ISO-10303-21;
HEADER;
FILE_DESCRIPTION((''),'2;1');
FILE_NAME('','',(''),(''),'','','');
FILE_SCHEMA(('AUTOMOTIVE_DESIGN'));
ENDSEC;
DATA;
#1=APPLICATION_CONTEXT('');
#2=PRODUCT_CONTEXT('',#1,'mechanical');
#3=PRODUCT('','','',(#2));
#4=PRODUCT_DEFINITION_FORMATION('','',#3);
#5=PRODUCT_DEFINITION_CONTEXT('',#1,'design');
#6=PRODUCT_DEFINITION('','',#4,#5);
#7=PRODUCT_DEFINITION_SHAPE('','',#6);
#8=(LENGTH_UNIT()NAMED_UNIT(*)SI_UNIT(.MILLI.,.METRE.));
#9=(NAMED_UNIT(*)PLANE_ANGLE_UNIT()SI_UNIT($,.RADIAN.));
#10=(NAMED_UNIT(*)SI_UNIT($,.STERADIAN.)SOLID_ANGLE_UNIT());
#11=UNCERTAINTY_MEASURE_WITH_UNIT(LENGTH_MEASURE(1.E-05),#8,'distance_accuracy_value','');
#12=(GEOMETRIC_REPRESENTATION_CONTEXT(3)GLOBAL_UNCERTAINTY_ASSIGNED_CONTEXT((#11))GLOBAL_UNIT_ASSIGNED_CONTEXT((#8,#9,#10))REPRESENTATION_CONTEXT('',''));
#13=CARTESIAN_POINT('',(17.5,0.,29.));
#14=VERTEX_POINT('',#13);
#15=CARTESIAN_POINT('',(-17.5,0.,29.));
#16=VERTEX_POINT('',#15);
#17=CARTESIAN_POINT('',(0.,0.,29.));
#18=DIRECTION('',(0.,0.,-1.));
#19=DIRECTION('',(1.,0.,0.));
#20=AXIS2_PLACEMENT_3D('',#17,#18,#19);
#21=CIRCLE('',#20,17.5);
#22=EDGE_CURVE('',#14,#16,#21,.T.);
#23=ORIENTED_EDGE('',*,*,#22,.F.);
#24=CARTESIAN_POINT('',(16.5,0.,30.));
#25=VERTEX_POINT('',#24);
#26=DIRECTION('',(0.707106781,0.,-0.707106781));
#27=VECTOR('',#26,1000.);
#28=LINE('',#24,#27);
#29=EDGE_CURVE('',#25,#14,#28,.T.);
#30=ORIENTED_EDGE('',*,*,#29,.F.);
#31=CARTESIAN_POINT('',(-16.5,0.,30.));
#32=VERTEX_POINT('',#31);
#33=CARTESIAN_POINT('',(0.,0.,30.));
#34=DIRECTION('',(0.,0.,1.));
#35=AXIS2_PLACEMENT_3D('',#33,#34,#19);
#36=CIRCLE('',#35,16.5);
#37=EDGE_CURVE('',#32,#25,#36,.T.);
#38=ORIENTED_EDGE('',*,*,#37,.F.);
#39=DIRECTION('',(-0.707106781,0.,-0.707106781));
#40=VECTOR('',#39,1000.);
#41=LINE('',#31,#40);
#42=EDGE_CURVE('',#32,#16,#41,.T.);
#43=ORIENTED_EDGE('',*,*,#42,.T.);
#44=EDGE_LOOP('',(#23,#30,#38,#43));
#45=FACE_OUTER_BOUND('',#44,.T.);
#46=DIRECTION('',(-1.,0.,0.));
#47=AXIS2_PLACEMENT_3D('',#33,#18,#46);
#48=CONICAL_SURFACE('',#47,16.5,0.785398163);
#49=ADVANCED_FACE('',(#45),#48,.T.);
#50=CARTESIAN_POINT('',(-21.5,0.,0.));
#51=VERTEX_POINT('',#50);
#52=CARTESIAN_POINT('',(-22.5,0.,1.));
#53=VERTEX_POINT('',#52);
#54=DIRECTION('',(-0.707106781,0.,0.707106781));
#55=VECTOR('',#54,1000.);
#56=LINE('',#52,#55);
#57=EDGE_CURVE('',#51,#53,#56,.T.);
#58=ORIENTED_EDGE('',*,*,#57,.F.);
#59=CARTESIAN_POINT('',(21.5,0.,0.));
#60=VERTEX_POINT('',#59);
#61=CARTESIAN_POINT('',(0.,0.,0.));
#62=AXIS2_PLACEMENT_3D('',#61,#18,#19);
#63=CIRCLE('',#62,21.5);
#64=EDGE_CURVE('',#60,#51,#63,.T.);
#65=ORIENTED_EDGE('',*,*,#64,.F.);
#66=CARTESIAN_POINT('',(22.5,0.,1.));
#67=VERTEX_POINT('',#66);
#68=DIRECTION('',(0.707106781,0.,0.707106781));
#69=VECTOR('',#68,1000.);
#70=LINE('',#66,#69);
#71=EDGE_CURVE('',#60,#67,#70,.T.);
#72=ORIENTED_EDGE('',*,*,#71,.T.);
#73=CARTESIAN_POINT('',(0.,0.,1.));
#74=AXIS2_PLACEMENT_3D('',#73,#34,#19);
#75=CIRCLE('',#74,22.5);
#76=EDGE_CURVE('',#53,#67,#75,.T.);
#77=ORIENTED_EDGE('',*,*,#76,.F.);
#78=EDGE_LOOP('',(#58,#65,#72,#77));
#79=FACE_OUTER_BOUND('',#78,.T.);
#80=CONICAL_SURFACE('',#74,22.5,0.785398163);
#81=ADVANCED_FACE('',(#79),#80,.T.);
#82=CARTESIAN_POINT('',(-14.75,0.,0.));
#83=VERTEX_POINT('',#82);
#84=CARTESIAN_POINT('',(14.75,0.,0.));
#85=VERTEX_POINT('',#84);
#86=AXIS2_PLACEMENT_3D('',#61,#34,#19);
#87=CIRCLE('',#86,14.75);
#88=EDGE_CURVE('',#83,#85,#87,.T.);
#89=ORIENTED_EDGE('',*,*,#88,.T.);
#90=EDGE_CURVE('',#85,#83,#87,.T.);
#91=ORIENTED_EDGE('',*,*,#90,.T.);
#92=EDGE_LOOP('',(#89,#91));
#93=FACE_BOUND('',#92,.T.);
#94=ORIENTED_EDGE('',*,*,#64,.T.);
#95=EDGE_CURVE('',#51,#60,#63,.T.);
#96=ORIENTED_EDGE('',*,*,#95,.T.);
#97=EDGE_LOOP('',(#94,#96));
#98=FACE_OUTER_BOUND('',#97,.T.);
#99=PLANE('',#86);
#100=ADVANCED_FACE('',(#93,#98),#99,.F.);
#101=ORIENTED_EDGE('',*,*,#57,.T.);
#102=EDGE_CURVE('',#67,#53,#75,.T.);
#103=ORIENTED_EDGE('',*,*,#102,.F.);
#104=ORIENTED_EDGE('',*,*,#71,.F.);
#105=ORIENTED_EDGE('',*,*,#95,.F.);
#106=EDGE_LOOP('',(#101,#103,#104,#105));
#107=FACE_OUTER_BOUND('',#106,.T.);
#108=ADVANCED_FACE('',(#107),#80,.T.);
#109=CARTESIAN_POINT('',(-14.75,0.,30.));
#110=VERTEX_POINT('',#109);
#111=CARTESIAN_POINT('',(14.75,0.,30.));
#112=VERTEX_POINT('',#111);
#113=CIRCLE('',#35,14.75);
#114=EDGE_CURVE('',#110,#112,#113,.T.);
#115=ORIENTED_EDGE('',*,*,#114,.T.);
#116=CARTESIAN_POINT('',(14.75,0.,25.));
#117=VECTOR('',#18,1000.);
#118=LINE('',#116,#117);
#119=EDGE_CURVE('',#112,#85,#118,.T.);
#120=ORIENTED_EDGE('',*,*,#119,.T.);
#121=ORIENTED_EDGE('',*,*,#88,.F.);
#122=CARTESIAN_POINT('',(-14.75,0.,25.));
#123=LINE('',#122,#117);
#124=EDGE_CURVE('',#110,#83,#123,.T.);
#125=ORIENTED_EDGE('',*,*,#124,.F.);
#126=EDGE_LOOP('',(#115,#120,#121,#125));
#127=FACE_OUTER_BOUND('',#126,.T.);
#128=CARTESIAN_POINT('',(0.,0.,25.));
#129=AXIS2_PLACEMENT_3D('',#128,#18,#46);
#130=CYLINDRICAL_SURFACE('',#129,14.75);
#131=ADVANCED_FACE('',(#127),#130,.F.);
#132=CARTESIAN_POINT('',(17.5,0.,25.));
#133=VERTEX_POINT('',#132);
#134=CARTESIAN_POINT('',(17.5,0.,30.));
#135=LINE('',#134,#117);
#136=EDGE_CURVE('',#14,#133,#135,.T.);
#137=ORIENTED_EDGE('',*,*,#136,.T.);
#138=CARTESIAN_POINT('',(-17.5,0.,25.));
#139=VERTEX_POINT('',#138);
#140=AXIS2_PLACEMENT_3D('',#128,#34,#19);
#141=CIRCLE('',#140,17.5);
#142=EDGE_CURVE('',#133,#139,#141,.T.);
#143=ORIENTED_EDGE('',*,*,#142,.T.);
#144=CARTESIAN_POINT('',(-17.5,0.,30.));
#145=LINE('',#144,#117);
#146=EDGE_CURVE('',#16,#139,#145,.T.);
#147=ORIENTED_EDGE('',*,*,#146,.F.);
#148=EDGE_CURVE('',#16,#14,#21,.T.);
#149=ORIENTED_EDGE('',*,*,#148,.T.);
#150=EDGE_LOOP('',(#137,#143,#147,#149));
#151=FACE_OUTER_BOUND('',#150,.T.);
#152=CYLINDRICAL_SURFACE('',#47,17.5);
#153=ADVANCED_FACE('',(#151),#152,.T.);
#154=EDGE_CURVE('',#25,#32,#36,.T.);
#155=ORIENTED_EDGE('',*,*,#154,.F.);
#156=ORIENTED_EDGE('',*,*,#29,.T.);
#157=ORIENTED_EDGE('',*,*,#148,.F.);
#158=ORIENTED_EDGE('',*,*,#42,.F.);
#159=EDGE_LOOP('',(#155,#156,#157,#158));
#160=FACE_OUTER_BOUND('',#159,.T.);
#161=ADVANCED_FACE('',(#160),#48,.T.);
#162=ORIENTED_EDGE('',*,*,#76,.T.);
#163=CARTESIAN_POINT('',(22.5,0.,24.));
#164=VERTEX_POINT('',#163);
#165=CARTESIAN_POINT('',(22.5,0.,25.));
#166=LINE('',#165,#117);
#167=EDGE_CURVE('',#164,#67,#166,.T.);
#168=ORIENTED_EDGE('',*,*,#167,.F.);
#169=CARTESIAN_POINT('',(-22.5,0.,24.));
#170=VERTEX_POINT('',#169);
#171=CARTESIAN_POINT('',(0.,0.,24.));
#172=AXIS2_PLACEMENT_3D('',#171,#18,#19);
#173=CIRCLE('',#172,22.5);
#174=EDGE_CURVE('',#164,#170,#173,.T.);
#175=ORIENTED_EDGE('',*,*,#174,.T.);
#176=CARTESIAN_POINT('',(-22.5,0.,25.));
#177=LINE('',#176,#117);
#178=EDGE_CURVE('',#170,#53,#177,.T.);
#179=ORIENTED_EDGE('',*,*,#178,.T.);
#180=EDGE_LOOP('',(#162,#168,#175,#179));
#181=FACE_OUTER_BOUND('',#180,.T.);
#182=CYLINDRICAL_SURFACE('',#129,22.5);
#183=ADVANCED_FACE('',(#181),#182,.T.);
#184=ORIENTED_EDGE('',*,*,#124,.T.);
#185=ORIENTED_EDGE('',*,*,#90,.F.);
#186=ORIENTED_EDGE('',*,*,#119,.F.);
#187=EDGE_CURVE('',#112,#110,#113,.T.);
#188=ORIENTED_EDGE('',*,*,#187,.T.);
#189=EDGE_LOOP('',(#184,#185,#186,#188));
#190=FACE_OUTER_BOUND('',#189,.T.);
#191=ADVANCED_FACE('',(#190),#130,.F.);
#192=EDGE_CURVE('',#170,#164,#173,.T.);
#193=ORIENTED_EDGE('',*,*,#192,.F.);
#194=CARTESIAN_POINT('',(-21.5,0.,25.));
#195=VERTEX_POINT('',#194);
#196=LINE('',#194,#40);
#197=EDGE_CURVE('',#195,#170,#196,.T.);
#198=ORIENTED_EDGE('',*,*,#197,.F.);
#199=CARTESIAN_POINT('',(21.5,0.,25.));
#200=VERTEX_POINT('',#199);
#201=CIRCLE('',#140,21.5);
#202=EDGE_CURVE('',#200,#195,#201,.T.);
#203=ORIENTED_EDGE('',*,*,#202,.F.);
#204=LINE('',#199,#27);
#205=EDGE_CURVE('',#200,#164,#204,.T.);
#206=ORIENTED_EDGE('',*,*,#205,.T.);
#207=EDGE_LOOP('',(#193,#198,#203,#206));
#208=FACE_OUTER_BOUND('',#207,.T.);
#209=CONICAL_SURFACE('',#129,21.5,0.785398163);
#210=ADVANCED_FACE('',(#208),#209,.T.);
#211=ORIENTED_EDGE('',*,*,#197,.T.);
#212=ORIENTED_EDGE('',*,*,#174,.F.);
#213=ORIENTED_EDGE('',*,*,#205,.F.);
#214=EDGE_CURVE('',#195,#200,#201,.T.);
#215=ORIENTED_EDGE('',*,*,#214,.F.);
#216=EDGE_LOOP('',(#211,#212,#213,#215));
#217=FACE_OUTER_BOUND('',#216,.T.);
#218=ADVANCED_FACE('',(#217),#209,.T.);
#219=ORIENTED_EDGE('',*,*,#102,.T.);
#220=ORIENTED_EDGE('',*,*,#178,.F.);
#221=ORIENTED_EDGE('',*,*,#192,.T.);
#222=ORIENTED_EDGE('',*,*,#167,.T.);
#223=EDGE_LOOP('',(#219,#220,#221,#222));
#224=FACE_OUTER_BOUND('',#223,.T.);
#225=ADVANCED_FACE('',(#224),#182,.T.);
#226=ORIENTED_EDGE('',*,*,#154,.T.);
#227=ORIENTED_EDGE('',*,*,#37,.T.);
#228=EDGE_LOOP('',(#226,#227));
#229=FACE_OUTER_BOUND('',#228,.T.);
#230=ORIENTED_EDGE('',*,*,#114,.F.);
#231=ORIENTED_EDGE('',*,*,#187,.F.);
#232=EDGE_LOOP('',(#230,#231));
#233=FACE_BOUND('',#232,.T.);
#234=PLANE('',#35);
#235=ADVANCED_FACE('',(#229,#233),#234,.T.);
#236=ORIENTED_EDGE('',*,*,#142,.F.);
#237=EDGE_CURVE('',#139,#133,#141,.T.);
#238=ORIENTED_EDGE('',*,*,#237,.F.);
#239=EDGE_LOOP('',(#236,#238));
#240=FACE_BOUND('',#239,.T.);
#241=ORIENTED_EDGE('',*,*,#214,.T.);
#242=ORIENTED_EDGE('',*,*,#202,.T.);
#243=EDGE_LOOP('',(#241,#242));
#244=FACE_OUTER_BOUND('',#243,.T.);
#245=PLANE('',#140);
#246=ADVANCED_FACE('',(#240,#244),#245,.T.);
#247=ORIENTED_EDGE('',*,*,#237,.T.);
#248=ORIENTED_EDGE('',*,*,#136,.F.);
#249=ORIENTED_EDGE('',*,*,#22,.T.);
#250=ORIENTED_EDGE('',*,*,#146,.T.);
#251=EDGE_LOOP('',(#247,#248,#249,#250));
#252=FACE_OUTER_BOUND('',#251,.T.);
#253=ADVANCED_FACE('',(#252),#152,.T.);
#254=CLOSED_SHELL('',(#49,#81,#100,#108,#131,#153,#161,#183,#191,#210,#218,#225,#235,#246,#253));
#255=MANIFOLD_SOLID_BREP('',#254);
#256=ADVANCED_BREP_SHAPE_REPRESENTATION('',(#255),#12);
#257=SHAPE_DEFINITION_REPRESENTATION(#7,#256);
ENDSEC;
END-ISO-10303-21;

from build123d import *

# Parameters (mm, degrees)
SKETCH1_R           = 22.5
SKETCH1_R_2         = 14.75
BOSS_EXTRUDE1_DEPTH = 25
SKETCH2_R           = 17.5
SKETCH2_R_2         = 14.75
BOSS_EXTRUDE2_DEPTH = 5
CHAMFER2_SIZE       = 1


with BuildPart() as part:
    # Sketch1 → Boss-Extrude1 (new body)
    with BuildSketch(Plane.XY):
        Circle(SKETCH1_R)
        Circle(SKETCH1_R_2, mode=Mode.SUBTRACT)
    extrude(amount=BOSS_EXTRUDE1_DEPTH)

    # Sketch2 → Boss-Extrude2 (add)
    with BuildSketch(Plane.XY.offset(25)):
        Circle(SKETCH2_R)
        Circle(SKETCH2_R_2, mode=Mode.SUBTRACT)
    extrude(amount=BOSS_EXTRUDE2_DEPTH)

    # Chamfer2
    chamfer2_edges = [part.edges().sort_by_distance(p)[0] for p in [
        (-17.5, 0, 30),
        (-22.5, 0, 0),
        (-22.5, 0, 25),
    ]]
    chamfer(chamfer2_edges, length=CHAMFER2_SIZE)


solid = part.part
